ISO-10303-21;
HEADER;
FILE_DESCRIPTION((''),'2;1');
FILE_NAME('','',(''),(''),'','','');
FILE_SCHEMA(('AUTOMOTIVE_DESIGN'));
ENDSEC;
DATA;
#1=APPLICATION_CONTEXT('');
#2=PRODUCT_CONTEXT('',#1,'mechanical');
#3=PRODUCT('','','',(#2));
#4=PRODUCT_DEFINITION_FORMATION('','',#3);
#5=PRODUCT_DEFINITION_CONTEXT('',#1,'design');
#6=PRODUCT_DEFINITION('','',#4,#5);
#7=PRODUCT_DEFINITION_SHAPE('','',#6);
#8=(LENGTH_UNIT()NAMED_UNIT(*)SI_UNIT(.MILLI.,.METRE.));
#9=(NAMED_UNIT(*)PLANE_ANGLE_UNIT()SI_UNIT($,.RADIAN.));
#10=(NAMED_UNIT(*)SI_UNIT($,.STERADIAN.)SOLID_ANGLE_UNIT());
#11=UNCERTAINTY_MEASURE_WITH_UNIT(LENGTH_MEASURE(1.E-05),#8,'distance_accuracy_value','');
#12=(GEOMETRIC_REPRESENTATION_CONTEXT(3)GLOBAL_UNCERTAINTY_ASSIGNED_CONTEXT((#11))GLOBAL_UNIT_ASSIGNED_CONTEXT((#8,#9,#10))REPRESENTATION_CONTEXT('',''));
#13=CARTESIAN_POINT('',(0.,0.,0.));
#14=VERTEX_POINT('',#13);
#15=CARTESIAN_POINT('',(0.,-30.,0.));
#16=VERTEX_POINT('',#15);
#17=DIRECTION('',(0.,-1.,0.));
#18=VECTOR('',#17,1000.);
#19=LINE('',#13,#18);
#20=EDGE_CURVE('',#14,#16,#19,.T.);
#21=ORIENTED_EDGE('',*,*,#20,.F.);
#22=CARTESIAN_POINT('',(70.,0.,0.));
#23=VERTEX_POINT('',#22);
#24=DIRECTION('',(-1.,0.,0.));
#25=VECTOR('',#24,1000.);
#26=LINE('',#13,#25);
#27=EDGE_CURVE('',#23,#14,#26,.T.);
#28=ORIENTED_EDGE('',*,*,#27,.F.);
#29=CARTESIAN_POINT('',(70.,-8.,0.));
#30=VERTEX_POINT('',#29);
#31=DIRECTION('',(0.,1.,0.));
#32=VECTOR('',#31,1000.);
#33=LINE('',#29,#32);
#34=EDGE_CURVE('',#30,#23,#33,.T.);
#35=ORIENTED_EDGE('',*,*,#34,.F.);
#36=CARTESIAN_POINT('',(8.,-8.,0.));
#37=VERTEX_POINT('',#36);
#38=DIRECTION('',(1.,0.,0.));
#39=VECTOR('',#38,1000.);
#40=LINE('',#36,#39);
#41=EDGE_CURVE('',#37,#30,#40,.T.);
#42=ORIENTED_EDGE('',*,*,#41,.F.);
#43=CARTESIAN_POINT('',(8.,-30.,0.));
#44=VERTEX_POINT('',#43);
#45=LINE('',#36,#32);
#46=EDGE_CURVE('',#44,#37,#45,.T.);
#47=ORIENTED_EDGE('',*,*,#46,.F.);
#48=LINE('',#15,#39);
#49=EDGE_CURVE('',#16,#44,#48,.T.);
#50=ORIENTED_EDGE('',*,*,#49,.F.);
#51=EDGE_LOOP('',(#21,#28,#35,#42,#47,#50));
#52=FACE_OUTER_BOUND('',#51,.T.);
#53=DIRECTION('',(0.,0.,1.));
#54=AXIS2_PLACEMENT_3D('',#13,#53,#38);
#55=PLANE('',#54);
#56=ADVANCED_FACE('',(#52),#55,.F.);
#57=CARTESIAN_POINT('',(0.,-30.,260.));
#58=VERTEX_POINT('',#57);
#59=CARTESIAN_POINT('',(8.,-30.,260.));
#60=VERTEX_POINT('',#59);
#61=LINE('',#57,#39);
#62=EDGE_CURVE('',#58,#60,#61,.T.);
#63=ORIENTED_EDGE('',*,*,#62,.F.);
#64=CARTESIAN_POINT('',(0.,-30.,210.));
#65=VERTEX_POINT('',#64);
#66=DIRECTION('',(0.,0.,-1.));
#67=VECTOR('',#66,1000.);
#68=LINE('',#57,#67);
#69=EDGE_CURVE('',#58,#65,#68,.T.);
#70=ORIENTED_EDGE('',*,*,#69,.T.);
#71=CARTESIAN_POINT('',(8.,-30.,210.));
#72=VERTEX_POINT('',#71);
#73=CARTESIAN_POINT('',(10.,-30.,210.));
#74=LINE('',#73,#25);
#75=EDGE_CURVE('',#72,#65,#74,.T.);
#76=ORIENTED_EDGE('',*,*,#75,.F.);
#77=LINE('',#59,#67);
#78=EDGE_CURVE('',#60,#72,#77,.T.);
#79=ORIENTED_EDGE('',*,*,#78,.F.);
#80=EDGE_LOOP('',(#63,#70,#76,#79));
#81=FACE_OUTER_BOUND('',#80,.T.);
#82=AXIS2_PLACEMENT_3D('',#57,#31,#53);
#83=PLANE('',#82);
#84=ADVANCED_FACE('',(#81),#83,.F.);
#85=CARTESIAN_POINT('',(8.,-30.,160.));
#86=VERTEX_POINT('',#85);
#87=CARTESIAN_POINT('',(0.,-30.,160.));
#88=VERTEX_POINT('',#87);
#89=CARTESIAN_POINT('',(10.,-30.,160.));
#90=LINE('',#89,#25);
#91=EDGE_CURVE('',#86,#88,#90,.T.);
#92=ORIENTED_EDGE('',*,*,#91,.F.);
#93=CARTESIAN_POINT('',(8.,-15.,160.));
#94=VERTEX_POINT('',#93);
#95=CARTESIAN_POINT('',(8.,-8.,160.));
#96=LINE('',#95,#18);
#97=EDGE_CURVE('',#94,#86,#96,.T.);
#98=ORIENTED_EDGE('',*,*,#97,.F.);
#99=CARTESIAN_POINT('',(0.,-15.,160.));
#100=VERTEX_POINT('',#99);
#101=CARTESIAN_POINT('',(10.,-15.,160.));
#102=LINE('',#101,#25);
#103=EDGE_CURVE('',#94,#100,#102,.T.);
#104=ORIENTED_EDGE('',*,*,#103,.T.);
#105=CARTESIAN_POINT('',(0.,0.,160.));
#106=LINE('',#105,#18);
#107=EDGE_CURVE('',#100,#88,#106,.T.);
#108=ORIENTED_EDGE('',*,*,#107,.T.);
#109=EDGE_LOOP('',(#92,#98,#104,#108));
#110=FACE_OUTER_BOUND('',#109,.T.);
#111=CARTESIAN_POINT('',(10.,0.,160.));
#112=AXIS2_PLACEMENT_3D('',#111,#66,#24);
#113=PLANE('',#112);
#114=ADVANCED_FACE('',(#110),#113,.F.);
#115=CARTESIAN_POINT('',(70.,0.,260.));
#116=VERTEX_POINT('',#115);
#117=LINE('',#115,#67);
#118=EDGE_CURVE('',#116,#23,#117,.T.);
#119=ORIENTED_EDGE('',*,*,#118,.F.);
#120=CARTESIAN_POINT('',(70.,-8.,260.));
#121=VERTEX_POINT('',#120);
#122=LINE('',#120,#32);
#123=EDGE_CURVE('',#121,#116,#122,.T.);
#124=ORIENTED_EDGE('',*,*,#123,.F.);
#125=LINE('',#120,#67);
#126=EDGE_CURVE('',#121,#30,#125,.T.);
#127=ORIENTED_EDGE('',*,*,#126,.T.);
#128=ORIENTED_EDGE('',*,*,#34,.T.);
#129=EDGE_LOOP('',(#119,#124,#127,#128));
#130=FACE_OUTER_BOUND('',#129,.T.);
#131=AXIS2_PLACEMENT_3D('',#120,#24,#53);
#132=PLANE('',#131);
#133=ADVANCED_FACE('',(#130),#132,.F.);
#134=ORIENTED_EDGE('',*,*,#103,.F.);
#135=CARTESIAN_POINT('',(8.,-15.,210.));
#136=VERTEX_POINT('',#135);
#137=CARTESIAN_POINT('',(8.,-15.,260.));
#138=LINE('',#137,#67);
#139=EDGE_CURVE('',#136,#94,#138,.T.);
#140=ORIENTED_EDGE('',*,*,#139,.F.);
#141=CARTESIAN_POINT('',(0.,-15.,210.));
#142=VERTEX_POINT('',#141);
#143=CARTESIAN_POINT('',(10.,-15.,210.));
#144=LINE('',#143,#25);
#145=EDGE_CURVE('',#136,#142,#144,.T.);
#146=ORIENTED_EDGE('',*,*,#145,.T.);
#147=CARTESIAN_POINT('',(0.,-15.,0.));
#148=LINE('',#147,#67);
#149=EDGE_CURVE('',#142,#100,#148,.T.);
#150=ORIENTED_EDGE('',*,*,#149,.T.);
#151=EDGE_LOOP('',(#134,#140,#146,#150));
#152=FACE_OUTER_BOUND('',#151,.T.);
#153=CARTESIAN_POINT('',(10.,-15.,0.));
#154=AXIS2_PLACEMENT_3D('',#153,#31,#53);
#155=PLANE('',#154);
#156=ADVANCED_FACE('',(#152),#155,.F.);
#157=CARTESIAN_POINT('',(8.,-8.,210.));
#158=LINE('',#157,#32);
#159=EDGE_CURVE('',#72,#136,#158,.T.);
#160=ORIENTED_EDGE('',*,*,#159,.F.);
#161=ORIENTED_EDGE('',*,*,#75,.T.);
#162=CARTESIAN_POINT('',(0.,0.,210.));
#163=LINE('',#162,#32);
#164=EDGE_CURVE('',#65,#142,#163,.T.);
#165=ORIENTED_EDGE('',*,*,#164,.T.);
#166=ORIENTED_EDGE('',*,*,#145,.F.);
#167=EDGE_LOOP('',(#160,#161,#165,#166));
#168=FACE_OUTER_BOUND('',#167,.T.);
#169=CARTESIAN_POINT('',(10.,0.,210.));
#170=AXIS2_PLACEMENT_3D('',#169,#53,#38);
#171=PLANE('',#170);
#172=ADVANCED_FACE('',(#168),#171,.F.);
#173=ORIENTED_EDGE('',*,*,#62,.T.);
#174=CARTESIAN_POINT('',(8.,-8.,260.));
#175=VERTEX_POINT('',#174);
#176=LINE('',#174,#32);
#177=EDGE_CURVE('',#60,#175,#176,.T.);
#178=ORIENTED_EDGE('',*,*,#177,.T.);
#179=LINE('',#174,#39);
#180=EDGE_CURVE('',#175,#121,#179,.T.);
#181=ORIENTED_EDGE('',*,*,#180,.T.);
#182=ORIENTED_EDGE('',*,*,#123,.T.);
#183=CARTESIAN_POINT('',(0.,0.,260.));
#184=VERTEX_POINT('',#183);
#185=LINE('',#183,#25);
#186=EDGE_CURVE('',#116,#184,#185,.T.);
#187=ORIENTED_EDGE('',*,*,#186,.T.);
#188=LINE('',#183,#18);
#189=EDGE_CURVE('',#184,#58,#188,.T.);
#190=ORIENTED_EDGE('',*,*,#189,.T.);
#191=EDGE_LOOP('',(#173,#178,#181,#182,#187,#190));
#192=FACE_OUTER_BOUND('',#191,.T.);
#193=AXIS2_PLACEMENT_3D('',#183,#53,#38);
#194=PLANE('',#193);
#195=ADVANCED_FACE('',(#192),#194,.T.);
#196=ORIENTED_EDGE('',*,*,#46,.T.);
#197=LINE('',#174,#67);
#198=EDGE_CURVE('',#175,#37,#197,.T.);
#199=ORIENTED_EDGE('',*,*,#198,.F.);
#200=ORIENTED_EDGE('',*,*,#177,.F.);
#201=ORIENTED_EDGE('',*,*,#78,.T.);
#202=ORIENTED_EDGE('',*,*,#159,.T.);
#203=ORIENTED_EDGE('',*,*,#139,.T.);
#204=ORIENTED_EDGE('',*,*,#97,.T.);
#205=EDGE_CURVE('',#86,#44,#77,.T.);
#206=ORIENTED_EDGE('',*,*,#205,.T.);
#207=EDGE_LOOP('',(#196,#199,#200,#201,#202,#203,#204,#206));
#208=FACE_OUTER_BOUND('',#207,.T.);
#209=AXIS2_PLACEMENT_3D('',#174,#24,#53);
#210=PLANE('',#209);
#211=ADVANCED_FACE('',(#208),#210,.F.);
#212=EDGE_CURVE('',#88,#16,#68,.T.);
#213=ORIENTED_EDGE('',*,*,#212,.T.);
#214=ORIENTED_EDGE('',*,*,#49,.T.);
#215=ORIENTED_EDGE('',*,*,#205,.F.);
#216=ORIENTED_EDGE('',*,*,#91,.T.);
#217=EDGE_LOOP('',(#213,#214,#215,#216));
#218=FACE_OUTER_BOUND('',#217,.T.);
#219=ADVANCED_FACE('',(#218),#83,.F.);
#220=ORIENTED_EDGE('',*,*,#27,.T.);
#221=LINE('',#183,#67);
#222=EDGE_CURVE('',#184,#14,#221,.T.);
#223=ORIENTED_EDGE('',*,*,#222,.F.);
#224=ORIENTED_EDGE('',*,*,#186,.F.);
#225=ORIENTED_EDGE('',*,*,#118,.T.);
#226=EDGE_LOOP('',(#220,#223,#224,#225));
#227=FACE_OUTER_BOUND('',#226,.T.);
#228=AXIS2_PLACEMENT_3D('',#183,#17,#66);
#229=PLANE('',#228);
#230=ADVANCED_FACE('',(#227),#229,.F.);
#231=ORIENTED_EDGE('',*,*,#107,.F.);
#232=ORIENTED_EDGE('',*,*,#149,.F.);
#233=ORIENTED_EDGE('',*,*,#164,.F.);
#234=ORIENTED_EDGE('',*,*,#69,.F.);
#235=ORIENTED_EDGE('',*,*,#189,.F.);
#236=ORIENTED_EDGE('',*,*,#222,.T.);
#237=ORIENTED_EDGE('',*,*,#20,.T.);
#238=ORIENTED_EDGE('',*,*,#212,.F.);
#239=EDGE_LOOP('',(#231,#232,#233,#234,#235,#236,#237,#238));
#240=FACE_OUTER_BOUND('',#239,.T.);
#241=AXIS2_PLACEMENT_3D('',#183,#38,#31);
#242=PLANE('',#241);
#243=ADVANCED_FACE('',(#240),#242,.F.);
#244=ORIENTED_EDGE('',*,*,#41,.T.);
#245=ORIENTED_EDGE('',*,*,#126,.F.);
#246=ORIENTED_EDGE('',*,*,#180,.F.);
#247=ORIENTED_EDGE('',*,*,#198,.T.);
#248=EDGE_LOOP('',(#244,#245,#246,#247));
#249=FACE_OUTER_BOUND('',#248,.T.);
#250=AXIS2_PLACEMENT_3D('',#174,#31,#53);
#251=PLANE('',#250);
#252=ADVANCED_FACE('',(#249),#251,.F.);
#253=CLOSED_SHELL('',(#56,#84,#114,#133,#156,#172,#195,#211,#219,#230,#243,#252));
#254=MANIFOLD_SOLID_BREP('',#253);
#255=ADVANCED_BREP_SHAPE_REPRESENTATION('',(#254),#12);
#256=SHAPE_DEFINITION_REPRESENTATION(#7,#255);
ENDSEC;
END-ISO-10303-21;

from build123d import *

# Parameters (mm, degrees)
EXTRUDE_1_DEPTH     = 260
SKETCH_2_W          = 50
SKETCH_2_H          = 15
CUT_EXTRUDE_1_DEPTH = 10


with BuildPart() as part:
    # 草图1 → 凸台-拉伸1 (new body)
    with BuildSketch(Plane.XY):
        Polygon((0, 0), (70, 0), (70, -8), (8, -8), (8, -30), (0, -30), align=None)
    extrude(amount=EXTRUDE_1_DEPTH)

    # 草图2 → 切除-拉伸1 (cut)
    with BuildSketch(Plane.ZY):
        with Locations((185, -22.5)):
            Rectangle(SKETCH_2_W, SKETCH_2_H)
    extrude(amount=-CUT_EXTRUDE_1_DEPTH, mode=Mode.SUBTRACT)


solid = part.part
